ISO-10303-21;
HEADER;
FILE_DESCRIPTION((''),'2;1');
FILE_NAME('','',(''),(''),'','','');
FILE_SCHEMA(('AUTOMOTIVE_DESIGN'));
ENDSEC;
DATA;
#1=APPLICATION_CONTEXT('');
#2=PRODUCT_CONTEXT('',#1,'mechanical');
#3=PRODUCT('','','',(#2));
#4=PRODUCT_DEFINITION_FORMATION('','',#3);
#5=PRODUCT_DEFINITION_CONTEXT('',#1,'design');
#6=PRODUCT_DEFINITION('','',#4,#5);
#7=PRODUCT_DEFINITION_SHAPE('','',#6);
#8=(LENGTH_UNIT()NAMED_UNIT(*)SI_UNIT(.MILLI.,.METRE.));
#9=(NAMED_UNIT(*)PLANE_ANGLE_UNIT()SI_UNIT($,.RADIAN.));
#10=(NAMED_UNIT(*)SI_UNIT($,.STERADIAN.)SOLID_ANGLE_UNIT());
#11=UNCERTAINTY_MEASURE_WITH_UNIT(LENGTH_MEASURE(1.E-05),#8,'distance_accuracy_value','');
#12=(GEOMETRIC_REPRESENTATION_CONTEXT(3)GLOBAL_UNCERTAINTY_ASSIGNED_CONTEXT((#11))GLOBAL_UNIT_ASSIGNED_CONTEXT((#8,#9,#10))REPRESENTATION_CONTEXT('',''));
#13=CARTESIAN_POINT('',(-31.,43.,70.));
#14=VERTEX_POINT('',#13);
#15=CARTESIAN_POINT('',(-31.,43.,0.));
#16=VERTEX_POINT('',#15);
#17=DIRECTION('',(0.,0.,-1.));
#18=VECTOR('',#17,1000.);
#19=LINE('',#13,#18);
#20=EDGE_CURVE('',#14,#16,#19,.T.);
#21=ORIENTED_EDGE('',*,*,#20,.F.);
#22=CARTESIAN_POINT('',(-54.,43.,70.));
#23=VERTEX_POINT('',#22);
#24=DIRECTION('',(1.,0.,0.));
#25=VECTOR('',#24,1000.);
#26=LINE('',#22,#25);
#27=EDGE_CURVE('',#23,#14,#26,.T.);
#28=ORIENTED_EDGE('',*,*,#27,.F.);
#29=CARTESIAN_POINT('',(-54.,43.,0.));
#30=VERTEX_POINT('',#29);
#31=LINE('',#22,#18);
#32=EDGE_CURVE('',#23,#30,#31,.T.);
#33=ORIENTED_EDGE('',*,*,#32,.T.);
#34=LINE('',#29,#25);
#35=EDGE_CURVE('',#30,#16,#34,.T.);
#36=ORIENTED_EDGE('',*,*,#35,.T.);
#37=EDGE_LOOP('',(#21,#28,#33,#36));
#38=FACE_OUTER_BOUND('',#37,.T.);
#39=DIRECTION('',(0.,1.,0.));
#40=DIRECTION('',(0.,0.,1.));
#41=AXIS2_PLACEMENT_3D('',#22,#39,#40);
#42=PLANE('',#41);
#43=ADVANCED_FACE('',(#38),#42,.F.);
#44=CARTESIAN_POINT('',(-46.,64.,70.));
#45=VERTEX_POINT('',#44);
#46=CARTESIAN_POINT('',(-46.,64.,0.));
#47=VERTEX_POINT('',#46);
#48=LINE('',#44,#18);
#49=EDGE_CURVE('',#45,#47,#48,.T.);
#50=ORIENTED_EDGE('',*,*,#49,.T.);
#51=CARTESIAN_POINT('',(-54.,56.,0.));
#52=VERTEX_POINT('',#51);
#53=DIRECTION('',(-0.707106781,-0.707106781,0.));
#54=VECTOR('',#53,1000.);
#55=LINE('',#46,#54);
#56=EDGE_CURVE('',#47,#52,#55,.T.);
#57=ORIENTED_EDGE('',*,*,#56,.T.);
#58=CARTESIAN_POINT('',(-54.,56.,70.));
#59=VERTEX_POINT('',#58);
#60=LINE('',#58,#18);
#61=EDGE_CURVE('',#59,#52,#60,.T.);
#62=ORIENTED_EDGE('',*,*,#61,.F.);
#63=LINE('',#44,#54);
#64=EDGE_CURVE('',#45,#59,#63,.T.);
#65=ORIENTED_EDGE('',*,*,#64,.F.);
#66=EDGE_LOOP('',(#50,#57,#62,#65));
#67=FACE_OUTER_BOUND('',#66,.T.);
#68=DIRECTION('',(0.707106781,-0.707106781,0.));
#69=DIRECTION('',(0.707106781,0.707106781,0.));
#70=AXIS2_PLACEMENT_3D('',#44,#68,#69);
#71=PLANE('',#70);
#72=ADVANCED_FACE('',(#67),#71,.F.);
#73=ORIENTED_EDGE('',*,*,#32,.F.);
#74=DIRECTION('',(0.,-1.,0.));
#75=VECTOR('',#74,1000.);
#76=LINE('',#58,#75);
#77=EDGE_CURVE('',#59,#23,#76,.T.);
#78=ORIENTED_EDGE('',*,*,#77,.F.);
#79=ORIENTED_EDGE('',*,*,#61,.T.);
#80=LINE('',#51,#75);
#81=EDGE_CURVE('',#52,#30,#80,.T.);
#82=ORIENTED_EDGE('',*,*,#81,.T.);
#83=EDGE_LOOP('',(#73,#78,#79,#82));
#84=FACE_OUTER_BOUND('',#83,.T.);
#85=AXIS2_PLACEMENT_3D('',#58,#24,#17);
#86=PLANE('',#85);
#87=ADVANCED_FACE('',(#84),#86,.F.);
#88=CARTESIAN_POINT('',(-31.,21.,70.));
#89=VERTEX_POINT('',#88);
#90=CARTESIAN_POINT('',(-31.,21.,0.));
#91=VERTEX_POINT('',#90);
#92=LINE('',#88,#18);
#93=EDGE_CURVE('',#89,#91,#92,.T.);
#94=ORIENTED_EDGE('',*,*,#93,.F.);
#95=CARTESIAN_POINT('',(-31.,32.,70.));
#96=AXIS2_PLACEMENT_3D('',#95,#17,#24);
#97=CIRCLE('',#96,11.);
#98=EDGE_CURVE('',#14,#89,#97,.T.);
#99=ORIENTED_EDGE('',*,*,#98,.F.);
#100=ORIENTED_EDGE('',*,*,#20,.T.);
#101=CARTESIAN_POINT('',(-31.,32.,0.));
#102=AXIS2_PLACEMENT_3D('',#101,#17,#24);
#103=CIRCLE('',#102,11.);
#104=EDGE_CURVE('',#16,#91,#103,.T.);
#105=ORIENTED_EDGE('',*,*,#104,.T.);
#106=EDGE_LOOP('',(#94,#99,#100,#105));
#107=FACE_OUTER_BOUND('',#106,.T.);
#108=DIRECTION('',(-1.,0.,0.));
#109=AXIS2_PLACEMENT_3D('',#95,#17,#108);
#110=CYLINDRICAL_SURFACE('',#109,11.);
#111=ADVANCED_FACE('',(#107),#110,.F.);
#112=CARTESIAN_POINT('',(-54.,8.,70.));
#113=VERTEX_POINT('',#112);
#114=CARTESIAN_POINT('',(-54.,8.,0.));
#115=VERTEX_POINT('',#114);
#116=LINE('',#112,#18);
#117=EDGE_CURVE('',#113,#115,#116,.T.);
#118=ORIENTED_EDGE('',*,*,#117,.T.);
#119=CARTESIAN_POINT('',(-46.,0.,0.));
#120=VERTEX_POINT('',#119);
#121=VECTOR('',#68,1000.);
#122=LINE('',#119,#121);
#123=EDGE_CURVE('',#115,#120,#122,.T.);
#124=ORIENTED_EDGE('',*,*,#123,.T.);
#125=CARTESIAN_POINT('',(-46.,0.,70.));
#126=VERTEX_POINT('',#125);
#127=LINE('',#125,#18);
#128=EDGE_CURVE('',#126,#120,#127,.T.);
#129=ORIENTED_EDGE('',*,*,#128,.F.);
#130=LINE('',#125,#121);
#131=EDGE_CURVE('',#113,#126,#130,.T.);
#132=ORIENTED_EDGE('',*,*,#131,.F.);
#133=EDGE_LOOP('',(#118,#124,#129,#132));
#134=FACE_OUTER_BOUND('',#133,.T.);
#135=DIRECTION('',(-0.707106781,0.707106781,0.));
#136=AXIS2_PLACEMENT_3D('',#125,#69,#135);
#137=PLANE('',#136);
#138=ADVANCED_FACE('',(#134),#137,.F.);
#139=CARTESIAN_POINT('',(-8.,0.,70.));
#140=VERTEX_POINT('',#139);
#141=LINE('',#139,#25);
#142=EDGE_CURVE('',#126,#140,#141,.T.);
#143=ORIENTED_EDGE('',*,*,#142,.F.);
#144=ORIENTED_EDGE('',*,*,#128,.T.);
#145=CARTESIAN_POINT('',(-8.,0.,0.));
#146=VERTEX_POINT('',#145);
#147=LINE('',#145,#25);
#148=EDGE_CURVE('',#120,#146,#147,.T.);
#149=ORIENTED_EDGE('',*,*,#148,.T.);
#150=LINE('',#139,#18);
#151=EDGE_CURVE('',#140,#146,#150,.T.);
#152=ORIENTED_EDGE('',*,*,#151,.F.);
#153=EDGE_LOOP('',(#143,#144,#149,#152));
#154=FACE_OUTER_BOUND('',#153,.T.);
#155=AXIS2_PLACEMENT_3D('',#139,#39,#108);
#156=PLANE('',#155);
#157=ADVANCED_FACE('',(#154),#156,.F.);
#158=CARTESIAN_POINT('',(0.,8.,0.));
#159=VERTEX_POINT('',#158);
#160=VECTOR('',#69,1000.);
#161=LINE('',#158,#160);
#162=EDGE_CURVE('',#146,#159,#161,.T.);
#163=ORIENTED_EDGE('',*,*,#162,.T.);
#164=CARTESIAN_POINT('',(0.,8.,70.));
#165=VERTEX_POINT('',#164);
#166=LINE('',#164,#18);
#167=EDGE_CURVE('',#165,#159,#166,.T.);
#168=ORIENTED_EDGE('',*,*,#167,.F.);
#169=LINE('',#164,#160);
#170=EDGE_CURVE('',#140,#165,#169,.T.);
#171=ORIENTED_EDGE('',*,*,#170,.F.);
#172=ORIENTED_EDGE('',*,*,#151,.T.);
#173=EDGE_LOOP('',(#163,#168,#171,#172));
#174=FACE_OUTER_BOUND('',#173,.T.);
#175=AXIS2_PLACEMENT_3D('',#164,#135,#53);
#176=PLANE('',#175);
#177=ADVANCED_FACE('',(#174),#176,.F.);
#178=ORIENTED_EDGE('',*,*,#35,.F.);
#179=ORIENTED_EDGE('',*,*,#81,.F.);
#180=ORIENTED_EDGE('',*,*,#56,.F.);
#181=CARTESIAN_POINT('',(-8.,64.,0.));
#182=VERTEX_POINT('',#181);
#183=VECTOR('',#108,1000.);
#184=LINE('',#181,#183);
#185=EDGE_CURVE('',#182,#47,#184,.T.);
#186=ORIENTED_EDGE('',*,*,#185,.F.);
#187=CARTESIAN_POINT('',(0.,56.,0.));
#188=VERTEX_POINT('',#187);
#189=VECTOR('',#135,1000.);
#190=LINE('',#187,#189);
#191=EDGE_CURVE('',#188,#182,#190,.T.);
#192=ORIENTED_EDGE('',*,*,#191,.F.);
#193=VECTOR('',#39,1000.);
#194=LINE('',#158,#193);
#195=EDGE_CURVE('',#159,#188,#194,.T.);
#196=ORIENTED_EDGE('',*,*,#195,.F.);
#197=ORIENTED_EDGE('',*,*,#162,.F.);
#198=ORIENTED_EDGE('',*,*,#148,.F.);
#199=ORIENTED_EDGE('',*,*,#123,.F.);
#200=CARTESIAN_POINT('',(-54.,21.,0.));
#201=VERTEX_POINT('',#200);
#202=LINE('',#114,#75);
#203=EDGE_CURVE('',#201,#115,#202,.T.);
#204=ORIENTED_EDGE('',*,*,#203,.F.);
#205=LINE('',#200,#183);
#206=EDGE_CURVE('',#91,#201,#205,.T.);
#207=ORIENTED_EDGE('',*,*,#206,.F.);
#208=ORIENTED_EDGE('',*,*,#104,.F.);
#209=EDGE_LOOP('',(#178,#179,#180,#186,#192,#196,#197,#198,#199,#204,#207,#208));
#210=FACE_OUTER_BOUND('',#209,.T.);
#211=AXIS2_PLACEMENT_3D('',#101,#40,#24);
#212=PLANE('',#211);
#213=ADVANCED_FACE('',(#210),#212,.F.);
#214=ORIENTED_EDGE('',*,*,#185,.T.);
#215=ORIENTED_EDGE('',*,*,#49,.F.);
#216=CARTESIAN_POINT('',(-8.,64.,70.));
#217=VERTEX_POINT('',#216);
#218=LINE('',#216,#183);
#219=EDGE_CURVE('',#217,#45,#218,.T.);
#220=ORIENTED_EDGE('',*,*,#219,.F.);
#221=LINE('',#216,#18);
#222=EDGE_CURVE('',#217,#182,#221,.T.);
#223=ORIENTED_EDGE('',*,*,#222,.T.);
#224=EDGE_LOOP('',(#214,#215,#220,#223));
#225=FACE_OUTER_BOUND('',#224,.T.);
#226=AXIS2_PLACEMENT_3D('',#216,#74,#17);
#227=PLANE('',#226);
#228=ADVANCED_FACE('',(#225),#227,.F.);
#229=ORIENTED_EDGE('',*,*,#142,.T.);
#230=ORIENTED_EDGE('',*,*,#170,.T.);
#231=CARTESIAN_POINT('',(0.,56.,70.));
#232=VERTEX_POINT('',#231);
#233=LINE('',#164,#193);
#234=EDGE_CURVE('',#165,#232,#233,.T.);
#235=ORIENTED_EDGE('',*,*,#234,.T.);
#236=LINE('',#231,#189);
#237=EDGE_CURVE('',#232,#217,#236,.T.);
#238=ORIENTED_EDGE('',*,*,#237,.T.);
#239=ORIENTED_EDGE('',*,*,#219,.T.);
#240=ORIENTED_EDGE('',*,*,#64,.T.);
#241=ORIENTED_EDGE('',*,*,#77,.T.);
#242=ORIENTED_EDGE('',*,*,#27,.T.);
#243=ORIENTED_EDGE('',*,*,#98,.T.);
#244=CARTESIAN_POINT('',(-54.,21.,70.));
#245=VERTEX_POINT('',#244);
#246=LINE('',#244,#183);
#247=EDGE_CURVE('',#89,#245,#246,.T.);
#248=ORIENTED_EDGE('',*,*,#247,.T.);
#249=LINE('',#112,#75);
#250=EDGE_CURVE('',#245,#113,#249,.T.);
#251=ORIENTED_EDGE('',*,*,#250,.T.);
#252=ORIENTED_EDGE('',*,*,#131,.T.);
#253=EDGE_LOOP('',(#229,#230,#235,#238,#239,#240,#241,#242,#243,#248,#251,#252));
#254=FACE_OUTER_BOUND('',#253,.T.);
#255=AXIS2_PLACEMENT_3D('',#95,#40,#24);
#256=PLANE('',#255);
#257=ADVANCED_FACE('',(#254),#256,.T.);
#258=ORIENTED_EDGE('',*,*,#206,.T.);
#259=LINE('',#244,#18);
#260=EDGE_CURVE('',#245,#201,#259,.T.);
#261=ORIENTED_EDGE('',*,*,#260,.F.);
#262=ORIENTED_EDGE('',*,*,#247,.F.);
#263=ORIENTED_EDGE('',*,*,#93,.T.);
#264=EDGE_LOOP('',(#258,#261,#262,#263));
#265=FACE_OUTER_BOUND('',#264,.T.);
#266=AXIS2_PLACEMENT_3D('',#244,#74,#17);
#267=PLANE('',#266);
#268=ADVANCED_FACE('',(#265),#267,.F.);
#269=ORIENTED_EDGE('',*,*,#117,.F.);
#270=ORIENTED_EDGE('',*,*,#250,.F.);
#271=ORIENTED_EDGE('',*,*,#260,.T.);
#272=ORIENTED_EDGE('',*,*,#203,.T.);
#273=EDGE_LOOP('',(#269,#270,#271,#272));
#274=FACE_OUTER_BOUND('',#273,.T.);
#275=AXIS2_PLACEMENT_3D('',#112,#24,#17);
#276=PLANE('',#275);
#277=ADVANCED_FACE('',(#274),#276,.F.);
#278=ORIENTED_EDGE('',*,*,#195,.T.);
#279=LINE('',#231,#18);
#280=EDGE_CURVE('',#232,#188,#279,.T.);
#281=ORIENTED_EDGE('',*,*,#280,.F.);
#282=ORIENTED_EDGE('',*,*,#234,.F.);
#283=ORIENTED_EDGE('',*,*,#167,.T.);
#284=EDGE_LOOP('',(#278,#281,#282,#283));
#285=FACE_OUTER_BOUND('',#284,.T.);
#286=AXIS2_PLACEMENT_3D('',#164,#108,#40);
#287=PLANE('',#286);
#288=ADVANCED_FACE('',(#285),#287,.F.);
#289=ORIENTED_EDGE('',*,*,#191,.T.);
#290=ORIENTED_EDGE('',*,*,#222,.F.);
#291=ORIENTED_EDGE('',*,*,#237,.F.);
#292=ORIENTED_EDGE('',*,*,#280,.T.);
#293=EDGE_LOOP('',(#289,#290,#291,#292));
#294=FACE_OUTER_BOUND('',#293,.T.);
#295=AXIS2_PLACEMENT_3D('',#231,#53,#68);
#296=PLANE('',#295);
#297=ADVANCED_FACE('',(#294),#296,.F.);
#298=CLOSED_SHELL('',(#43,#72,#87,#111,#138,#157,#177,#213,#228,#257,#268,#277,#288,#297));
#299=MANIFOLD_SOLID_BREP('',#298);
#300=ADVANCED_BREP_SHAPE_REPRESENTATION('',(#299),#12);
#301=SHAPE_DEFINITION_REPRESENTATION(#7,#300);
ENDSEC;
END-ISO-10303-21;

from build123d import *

# Parameters (mm, degrees)
BOSS_EXTRUDE1_DEPTH = 70


with BuildPart() as part:
    # Sketch1 → Boss-Extrude1 (new body)
    with BuildSketch(Plane.XY):
        with BuildLine():
            Line((0, 8), (0, 56))
            Line((0, 56), (-8, 64))
            Line((-8, 64), (-46, 64))
            Line((-46, 64), (-54, 56))
            Line((-54, 56), (-54, 43))
            Line((-54, 43), (-31, 43))
            ThreePointArc((-31, 43), (-20, 32), (-31, 21))
            Line((-31, 21), (-54, 21))
            Line((-54, 21), (-54, 8))
            Line((-54, 8), (-46, 0))
            Line((-46, 0), (-8, 0))
            Line((-8, 0), (0, 8))
        make_face()
    extrude(amount=BOSS_EXTRUDE1_DEPTH)


solid = part.part
